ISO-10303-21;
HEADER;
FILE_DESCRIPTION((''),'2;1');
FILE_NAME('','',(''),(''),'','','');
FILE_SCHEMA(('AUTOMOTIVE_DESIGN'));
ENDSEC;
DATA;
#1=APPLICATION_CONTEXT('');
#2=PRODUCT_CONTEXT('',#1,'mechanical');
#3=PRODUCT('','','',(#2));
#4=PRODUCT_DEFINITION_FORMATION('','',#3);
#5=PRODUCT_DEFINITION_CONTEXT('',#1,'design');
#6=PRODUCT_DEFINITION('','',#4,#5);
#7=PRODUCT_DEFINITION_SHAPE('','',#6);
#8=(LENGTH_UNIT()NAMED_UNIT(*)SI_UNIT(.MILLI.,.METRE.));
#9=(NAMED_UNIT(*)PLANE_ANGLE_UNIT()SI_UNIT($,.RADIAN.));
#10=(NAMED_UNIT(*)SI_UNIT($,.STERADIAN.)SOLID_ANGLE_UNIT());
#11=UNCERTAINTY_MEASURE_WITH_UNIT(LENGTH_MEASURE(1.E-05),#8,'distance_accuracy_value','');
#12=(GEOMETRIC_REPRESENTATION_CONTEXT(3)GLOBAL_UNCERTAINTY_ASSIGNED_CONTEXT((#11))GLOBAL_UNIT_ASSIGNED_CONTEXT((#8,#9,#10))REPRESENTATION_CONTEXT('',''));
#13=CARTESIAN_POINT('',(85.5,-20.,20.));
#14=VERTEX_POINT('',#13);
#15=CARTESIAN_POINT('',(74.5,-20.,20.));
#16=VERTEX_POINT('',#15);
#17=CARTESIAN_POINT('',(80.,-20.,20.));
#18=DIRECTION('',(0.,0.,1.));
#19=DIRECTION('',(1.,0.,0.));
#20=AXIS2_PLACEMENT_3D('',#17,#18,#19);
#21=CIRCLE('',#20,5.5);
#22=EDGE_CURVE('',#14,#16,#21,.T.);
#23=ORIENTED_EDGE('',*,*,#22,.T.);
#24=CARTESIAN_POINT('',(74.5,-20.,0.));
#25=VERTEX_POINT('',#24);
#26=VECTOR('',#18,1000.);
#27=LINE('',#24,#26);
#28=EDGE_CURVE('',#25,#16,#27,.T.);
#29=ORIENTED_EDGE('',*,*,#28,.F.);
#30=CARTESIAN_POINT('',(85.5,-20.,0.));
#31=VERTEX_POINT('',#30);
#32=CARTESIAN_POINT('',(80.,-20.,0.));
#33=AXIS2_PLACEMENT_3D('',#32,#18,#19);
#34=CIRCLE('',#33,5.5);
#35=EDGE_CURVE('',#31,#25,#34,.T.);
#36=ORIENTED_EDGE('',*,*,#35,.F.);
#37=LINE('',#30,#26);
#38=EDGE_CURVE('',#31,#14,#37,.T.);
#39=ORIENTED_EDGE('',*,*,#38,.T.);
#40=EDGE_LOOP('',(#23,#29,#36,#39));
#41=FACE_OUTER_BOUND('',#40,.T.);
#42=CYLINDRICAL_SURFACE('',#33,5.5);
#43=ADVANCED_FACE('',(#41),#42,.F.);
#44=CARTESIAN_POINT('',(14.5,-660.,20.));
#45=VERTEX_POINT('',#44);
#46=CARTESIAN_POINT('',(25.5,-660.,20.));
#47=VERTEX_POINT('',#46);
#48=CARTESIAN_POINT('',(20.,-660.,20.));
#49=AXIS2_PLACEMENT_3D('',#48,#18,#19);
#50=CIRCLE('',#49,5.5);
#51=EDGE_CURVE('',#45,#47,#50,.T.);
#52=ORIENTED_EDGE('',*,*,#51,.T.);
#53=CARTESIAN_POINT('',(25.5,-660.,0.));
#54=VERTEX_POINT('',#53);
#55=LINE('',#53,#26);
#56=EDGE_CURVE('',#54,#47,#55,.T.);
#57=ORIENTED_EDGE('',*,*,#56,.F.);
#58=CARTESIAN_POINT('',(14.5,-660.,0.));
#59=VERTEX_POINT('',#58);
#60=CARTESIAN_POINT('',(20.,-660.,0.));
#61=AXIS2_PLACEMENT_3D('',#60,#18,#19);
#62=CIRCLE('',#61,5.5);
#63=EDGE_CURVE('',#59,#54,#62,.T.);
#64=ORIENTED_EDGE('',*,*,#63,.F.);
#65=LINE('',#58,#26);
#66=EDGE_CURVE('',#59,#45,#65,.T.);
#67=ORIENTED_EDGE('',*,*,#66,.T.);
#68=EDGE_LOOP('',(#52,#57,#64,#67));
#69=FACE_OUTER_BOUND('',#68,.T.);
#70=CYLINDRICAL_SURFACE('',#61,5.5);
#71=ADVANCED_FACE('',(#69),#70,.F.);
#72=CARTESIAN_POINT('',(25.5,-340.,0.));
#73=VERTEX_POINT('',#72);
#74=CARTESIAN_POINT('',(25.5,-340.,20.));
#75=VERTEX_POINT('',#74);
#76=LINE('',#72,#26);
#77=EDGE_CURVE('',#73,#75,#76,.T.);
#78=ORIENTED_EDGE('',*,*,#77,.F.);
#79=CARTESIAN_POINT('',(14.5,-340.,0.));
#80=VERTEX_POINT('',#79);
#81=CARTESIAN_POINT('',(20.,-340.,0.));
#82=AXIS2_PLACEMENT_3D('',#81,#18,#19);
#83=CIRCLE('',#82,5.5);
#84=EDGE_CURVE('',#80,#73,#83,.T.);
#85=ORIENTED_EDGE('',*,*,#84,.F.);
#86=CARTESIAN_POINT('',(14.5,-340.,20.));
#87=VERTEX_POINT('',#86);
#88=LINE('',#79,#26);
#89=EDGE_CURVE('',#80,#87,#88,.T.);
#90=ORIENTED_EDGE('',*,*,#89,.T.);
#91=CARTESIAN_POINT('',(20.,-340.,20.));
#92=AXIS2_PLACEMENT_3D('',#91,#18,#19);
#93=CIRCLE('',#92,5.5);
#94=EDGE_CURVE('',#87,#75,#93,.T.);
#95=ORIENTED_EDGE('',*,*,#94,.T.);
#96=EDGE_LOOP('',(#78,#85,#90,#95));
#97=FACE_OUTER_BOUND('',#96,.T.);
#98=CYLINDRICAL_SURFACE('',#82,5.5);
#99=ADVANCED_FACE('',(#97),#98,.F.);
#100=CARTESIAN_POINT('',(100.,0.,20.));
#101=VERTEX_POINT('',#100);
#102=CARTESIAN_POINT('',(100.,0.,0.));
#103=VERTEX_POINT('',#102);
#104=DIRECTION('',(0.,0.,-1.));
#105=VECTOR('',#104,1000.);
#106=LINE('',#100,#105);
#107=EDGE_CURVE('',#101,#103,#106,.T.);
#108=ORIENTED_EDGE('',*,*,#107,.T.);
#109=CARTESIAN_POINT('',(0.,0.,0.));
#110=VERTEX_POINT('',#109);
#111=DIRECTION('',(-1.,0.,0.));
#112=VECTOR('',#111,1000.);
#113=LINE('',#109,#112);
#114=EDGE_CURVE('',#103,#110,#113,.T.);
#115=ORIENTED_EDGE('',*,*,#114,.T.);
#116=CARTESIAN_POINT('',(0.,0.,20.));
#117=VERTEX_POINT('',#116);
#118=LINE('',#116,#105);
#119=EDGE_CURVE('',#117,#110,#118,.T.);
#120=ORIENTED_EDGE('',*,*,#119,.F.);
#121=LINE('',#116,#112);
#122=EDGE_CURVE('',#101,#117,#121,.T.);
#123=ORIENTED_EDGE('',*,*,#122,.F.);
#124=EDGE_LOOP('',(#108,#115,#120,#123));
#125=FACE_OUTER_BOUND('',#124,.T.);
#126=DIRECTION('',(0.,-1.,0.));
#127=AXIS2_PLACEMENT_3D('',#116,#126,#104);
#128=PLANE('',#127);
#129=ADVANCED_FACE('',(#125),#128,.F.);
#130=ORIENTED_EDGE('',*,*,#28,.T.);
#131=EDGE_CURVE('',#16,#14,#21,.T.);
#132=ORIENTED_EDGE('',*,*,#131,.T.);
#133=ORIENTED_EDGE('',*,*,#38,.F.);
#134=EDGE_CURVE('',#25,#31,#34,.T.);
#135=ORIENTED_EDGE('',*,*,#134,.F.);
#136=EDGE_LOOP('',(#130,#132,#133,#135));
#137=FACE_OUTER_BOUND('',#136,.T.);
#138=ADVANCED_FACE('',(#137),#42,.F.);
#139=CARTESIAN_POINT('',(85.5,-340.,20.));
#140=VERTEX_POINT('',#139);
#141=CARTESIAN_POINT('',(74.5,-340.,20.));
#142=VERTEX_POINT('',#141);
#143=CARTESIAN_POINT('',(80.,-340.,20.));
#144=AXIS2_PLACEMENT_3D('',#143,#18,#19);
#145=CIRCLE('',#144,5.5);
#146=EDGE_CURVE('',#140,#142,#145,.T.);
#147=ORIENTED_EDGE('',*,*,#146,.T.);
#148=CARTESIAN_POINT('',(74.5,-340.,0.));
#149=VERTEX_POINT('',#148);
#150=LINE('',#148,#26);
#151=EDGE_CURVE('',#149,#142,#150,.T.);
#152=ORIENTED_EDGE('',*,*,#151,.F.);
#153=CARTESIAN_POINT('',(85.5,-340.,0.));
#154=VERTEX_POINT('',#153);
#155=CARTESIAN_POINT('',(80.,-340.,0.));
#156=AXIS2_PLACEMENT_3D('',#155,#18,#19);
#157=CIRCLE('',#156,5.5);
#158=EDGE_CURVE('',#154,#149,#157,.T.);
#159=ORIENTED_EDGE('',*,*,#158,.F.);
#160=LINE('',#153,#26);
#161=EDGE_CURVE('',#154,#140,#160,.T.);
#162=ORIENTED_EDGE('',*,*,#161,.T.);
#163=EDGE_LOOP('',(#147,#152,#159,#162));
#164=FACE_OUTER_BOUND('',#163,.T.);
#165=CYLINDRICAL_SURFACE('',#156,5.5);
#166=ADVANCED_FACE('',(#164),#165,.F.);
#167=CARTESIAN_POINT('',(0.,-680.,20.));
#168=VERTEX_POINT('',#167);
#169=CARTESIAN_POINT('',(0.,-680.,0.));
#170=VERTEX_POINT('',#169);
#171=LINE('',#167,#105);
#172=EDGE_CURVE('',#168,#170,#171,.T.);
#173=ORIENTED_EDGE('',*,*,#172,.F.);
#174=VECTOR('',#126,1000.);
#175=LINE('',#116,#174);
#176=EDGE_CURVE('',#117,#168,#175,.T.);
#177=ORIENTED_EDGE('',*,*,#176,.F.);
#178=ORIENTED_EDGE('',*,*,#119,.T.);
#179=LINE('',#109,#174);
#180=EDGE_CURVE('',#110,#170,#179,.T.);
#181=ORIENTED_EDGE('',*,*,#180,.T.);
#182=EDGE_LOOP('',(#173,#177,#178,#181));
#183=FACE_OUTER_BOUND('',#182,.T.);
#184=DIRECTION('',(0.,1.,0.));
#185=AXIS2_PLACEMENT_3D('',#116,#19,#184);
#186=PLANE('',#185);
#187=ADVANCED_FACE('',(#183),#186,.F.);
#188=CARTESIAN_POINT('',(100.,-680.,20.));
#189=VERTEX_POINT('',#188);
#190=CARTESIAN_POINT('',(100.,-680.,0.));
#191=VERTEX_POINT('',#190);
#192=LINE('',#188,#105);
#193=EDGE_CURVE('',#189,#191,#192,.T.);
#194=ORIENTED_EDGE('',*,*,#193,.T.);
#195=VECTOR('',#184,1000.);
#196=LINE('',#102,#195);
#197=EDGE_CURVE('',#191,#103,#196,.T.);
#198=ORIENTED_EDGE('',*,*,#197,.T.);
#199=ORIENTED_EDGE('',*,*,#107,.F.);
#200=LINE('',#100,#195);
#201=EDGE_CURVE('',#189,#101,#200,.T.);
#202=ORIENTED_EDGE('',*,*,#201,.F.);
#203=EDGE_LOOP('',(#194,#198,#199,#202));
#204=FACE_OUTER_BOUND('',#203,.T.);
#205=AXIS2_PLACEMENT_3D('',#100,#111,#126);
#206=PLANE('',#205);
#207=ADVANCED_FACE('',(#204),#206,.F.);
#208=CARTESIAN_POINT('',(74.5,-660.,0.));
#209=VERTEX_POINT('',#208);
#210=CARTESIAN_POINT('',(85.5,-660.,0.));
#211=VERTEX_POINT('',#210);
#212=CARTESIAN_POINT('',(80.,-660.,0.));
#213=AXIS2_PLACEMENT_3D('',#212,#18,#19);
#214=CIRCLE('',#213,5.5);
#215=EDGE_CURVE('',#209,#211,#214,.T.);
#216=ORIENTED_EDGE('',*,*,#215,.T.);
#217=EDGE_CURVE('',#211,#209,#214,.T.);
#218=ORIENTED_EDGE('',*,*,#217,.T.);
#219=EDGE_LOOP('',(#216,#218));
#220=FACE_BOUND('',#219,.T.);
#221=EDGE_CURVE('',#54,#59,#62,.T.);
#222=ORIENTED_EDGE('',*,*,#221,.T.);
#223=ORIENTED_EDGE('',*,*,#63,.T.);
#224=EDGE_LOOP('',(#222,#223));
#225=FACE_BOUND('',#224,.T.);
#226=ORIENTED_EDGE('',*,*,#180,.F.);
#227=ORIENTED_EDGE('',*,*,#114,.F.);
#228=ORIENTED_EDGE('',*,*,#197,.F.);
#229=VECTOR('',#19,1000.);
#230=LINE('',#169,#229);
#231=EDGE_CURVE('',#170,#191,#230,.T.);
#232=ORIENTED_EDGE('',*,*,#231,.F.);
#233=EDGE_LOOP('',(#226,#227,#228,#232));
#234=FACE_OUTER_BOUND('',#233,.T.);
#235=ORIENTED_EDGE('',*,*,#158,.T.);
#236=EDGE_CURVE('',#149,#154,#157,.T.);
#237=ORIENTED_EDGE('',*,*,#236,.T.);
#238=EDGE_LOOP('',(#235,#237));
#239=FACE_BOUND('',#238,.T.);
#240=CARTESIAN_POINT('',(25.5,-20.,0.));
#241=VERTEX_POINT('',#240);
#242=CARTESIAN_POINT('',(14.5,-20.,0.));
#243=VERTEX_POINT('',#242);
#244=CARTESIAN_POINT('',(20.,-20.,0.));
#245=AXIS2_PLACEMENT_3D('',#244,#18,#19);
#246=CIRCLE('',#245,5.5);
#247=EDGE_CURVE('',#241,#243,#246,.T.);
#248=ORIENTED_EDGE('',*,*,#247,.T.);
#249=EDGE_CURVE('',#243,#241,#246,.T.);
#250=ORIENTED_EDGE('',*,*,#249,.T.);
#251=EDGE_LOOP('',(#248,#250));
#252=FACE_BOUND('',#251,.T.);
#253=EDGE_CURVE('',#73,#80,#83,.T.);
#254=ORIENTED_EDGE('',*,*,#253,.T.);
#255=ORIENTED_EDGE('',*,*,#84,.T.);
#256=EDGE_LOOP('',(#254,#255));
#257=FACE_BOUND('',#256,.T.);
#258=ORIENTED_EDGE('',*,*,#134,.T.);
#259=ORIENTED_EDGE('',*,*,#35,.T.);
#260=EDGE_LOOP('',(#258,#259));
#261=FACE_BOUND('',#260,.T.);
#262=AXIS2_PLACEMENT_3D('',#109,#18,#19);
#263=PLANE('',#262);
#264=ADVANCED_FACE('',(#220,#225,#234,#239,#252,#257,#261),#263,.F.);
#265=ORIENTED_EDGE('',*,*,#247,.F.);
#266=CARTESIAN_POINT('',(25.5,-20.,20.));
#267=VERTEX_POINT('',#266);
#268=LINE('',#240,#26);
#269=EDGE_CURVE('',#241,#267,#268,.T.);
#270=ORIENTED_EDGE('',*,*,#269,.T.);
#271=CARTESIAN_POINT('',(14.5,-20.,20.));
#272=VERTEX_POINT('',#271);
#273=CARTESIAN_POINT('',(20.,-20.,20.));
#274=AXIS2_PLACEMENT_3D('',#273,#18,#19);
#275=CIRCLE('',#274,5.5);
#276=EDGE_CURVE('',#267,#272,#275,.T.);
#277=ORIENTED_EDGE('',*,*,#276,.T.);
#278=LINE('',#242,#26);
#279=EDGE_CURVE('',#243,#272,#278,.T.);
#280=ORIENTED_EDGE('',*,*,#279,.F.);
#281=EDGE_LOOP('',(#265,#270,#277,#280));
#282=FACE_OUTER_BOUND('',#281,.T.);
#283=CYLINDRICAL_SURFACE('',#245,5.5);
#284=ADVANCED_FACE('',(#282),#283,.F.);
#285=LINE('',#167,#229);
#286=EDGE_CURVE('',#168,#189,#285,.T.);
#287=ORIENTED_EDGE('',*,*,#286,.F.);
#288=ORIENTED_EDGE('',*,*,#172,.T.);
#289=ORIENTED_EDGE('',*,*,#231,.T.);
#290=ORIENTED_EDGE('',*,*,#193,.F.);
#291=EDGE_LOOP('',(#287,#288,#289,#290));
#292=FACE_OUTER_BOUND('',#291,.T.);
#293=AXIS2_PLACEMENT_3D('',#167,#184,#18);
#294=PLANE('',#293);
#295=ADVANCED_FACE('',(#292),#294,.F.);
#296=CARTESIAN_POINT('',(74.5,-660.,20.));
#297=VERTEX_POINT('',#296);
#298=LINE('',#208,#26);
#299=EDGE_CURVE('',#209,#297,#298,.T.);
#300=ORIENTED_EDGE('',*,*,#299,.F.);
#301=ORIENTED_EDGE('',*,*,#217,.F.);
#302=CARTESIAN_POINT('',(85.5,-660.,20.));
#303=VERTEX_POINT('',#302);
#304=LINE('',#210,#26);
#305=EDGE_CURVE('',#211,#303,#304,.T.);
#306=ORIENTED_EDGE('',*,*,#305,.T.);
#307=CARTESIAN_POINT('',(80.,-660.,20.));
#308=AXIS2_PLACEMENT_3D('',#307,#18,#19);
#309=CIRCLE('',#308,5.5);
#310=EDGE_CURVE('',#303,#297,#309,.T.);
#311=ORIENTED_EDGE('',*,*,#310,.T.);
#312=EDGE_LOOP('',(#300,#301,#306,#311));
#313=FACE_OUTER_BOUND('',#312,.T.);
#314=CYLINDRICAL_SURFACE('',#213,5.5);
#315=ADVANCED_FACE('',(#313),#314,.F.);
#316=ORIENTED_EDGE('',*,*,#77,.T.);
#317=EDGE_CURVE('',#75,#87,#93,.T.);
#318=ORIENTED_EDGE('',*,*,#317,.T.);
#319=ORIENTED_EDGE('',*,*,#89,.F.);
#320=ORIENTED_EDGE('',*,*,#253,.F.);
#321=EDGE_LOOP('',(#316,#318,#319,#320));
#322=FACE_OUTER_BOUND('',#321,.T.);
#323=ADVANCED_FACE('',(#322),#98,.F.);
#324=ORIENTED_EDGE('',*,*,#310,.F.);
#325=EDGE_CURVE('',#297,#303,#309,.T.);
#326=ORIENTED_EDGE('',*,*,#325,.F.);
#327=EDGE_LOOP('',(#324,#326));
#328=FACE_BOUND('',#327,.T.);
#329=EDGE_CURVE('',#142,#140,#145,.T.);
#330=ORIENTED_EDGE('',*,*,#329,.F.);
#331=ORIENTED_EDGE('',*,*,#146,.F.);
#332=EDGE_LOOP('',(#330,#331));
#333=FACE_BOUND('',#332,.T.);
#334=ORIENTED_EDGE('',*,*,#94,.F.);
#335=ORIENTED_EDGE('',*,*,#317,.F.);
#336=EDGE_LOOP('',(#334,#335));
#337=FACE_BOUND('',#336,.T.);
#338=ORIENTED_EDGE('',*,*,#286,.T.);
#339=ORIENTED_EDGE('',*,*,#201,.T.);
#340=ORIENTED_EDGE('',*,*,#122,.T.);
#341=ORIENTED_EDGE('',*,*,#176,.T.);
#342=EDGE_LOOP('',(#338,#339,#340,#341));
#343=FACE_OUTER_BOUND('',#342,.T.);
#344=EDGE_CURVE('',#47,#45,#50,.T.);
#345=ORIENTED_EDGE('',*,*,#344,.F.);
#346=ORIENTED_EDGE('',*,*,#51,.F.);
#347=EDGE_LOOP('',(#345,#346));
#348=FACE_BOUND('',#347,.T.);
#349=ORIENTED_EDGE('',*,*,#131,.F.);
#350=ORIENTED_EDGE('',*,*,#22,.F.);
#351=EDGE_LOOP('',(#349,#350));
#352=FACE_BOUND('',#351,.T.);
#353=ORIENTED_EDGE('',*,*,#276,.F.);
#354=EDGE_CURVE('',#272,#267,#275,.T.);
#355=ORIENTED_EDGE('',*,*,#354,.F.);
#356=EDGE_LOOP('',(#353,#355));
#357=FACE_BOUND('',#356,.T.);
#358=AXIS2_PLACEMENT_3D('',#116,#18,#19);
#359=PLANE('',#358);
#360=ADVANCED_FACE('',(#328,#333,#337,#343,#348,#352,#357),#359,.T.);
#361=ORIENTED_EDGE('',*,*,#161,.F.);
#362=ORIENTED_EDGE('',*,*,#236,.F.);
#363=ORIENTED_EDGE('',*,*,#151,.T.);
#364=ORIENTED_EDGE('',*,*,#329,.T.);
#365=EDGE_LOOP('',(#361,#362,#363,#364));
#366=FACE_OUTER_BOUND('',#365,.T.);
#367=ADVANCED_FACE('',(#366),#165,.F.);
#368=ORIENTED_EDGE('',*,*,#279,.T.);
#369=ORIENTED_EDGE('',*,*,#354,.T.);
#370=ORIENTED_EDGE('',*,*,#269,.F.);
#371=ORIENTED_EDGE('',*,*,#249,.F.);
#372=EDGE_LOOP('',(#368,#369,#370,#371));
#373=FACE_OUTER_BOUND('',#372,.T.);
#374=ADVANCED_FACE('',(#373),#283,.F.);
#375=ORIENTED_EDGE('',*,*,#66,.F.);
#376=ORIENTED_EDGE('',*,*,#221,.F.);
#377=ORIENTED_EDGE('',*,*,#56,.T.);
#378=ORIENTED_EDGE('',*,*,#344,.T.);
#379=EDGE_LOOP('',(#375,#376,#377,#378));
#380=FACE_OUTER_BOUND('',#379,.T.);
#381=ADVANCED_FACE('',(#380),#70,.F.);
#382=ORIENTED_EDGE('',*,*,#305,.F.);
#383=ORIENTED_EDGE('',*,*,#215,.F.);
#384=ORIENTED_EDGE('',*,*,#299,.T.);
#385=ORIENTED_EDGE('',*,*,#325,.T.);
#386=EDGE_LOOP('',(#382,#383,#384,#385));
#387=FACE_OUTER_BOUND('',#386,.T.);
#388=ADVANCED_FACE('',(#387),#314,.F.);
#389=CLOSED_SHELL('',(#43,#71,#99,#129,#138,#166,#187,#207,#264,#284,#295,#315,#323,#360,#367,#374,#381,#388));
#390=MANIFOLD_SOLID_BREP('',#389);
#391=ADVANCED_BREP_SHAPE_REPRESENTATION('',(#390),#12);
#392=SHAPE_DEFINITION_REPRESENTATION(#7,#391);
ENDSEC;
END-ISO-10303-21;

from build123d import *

# Parameters (mm, degrees)
SKETCH1_W            = 100
SKETCH1_H            = 680
BOSS_EXTRUDE1_DEPTH  = 20
SKETCH2_R            = 5.5
CUT_EXTRUDE1_DEPTH   = 20
LPATTERN1_COUNT      = 2
LPATTERN1_PITCH      = 60
LPATTERN1_COUNT_DIR2 = 3
LPATTERN1_PITCH_DIR2 = 320


with BuildPart() as part:
    # Sketch1 → Boss-Extrude1 (new body)
    with BuildSketch(Plane.XY):
        with Locations((50, -340)):
            Rectangle(SKETCH1_W, SKETCH1_H)
    extrude(amount=BOSS_EXTRUDE1_DEPTH)

    # Sketch2 → Cut-Extrude1 (cut)
    with BuildSketch(Plane.XY.offset(20)):
        with Locations((20, -20)):
            Circle(SKETCH2_R)
    cut_extrude1 = extrude(amount=-CUT_EXTRUDE1_DEPTH, mode=Mode.SUBTRACT)

    # LPattern1: Cut-Extrude1 2 × 3
    with Locations(*[(i * LPATTERN1_PITCH, -j * LPATTERN1_PITCH_DIR2, 0) for i in range(LPATTERN1_COUNT) for j in range(LPATTERN1_COUNT_DIR2) if (i, j) != (0, 0)]):
        add(cut_extrude1, mode=Mode.SUBTRACT)


solid = part.part
